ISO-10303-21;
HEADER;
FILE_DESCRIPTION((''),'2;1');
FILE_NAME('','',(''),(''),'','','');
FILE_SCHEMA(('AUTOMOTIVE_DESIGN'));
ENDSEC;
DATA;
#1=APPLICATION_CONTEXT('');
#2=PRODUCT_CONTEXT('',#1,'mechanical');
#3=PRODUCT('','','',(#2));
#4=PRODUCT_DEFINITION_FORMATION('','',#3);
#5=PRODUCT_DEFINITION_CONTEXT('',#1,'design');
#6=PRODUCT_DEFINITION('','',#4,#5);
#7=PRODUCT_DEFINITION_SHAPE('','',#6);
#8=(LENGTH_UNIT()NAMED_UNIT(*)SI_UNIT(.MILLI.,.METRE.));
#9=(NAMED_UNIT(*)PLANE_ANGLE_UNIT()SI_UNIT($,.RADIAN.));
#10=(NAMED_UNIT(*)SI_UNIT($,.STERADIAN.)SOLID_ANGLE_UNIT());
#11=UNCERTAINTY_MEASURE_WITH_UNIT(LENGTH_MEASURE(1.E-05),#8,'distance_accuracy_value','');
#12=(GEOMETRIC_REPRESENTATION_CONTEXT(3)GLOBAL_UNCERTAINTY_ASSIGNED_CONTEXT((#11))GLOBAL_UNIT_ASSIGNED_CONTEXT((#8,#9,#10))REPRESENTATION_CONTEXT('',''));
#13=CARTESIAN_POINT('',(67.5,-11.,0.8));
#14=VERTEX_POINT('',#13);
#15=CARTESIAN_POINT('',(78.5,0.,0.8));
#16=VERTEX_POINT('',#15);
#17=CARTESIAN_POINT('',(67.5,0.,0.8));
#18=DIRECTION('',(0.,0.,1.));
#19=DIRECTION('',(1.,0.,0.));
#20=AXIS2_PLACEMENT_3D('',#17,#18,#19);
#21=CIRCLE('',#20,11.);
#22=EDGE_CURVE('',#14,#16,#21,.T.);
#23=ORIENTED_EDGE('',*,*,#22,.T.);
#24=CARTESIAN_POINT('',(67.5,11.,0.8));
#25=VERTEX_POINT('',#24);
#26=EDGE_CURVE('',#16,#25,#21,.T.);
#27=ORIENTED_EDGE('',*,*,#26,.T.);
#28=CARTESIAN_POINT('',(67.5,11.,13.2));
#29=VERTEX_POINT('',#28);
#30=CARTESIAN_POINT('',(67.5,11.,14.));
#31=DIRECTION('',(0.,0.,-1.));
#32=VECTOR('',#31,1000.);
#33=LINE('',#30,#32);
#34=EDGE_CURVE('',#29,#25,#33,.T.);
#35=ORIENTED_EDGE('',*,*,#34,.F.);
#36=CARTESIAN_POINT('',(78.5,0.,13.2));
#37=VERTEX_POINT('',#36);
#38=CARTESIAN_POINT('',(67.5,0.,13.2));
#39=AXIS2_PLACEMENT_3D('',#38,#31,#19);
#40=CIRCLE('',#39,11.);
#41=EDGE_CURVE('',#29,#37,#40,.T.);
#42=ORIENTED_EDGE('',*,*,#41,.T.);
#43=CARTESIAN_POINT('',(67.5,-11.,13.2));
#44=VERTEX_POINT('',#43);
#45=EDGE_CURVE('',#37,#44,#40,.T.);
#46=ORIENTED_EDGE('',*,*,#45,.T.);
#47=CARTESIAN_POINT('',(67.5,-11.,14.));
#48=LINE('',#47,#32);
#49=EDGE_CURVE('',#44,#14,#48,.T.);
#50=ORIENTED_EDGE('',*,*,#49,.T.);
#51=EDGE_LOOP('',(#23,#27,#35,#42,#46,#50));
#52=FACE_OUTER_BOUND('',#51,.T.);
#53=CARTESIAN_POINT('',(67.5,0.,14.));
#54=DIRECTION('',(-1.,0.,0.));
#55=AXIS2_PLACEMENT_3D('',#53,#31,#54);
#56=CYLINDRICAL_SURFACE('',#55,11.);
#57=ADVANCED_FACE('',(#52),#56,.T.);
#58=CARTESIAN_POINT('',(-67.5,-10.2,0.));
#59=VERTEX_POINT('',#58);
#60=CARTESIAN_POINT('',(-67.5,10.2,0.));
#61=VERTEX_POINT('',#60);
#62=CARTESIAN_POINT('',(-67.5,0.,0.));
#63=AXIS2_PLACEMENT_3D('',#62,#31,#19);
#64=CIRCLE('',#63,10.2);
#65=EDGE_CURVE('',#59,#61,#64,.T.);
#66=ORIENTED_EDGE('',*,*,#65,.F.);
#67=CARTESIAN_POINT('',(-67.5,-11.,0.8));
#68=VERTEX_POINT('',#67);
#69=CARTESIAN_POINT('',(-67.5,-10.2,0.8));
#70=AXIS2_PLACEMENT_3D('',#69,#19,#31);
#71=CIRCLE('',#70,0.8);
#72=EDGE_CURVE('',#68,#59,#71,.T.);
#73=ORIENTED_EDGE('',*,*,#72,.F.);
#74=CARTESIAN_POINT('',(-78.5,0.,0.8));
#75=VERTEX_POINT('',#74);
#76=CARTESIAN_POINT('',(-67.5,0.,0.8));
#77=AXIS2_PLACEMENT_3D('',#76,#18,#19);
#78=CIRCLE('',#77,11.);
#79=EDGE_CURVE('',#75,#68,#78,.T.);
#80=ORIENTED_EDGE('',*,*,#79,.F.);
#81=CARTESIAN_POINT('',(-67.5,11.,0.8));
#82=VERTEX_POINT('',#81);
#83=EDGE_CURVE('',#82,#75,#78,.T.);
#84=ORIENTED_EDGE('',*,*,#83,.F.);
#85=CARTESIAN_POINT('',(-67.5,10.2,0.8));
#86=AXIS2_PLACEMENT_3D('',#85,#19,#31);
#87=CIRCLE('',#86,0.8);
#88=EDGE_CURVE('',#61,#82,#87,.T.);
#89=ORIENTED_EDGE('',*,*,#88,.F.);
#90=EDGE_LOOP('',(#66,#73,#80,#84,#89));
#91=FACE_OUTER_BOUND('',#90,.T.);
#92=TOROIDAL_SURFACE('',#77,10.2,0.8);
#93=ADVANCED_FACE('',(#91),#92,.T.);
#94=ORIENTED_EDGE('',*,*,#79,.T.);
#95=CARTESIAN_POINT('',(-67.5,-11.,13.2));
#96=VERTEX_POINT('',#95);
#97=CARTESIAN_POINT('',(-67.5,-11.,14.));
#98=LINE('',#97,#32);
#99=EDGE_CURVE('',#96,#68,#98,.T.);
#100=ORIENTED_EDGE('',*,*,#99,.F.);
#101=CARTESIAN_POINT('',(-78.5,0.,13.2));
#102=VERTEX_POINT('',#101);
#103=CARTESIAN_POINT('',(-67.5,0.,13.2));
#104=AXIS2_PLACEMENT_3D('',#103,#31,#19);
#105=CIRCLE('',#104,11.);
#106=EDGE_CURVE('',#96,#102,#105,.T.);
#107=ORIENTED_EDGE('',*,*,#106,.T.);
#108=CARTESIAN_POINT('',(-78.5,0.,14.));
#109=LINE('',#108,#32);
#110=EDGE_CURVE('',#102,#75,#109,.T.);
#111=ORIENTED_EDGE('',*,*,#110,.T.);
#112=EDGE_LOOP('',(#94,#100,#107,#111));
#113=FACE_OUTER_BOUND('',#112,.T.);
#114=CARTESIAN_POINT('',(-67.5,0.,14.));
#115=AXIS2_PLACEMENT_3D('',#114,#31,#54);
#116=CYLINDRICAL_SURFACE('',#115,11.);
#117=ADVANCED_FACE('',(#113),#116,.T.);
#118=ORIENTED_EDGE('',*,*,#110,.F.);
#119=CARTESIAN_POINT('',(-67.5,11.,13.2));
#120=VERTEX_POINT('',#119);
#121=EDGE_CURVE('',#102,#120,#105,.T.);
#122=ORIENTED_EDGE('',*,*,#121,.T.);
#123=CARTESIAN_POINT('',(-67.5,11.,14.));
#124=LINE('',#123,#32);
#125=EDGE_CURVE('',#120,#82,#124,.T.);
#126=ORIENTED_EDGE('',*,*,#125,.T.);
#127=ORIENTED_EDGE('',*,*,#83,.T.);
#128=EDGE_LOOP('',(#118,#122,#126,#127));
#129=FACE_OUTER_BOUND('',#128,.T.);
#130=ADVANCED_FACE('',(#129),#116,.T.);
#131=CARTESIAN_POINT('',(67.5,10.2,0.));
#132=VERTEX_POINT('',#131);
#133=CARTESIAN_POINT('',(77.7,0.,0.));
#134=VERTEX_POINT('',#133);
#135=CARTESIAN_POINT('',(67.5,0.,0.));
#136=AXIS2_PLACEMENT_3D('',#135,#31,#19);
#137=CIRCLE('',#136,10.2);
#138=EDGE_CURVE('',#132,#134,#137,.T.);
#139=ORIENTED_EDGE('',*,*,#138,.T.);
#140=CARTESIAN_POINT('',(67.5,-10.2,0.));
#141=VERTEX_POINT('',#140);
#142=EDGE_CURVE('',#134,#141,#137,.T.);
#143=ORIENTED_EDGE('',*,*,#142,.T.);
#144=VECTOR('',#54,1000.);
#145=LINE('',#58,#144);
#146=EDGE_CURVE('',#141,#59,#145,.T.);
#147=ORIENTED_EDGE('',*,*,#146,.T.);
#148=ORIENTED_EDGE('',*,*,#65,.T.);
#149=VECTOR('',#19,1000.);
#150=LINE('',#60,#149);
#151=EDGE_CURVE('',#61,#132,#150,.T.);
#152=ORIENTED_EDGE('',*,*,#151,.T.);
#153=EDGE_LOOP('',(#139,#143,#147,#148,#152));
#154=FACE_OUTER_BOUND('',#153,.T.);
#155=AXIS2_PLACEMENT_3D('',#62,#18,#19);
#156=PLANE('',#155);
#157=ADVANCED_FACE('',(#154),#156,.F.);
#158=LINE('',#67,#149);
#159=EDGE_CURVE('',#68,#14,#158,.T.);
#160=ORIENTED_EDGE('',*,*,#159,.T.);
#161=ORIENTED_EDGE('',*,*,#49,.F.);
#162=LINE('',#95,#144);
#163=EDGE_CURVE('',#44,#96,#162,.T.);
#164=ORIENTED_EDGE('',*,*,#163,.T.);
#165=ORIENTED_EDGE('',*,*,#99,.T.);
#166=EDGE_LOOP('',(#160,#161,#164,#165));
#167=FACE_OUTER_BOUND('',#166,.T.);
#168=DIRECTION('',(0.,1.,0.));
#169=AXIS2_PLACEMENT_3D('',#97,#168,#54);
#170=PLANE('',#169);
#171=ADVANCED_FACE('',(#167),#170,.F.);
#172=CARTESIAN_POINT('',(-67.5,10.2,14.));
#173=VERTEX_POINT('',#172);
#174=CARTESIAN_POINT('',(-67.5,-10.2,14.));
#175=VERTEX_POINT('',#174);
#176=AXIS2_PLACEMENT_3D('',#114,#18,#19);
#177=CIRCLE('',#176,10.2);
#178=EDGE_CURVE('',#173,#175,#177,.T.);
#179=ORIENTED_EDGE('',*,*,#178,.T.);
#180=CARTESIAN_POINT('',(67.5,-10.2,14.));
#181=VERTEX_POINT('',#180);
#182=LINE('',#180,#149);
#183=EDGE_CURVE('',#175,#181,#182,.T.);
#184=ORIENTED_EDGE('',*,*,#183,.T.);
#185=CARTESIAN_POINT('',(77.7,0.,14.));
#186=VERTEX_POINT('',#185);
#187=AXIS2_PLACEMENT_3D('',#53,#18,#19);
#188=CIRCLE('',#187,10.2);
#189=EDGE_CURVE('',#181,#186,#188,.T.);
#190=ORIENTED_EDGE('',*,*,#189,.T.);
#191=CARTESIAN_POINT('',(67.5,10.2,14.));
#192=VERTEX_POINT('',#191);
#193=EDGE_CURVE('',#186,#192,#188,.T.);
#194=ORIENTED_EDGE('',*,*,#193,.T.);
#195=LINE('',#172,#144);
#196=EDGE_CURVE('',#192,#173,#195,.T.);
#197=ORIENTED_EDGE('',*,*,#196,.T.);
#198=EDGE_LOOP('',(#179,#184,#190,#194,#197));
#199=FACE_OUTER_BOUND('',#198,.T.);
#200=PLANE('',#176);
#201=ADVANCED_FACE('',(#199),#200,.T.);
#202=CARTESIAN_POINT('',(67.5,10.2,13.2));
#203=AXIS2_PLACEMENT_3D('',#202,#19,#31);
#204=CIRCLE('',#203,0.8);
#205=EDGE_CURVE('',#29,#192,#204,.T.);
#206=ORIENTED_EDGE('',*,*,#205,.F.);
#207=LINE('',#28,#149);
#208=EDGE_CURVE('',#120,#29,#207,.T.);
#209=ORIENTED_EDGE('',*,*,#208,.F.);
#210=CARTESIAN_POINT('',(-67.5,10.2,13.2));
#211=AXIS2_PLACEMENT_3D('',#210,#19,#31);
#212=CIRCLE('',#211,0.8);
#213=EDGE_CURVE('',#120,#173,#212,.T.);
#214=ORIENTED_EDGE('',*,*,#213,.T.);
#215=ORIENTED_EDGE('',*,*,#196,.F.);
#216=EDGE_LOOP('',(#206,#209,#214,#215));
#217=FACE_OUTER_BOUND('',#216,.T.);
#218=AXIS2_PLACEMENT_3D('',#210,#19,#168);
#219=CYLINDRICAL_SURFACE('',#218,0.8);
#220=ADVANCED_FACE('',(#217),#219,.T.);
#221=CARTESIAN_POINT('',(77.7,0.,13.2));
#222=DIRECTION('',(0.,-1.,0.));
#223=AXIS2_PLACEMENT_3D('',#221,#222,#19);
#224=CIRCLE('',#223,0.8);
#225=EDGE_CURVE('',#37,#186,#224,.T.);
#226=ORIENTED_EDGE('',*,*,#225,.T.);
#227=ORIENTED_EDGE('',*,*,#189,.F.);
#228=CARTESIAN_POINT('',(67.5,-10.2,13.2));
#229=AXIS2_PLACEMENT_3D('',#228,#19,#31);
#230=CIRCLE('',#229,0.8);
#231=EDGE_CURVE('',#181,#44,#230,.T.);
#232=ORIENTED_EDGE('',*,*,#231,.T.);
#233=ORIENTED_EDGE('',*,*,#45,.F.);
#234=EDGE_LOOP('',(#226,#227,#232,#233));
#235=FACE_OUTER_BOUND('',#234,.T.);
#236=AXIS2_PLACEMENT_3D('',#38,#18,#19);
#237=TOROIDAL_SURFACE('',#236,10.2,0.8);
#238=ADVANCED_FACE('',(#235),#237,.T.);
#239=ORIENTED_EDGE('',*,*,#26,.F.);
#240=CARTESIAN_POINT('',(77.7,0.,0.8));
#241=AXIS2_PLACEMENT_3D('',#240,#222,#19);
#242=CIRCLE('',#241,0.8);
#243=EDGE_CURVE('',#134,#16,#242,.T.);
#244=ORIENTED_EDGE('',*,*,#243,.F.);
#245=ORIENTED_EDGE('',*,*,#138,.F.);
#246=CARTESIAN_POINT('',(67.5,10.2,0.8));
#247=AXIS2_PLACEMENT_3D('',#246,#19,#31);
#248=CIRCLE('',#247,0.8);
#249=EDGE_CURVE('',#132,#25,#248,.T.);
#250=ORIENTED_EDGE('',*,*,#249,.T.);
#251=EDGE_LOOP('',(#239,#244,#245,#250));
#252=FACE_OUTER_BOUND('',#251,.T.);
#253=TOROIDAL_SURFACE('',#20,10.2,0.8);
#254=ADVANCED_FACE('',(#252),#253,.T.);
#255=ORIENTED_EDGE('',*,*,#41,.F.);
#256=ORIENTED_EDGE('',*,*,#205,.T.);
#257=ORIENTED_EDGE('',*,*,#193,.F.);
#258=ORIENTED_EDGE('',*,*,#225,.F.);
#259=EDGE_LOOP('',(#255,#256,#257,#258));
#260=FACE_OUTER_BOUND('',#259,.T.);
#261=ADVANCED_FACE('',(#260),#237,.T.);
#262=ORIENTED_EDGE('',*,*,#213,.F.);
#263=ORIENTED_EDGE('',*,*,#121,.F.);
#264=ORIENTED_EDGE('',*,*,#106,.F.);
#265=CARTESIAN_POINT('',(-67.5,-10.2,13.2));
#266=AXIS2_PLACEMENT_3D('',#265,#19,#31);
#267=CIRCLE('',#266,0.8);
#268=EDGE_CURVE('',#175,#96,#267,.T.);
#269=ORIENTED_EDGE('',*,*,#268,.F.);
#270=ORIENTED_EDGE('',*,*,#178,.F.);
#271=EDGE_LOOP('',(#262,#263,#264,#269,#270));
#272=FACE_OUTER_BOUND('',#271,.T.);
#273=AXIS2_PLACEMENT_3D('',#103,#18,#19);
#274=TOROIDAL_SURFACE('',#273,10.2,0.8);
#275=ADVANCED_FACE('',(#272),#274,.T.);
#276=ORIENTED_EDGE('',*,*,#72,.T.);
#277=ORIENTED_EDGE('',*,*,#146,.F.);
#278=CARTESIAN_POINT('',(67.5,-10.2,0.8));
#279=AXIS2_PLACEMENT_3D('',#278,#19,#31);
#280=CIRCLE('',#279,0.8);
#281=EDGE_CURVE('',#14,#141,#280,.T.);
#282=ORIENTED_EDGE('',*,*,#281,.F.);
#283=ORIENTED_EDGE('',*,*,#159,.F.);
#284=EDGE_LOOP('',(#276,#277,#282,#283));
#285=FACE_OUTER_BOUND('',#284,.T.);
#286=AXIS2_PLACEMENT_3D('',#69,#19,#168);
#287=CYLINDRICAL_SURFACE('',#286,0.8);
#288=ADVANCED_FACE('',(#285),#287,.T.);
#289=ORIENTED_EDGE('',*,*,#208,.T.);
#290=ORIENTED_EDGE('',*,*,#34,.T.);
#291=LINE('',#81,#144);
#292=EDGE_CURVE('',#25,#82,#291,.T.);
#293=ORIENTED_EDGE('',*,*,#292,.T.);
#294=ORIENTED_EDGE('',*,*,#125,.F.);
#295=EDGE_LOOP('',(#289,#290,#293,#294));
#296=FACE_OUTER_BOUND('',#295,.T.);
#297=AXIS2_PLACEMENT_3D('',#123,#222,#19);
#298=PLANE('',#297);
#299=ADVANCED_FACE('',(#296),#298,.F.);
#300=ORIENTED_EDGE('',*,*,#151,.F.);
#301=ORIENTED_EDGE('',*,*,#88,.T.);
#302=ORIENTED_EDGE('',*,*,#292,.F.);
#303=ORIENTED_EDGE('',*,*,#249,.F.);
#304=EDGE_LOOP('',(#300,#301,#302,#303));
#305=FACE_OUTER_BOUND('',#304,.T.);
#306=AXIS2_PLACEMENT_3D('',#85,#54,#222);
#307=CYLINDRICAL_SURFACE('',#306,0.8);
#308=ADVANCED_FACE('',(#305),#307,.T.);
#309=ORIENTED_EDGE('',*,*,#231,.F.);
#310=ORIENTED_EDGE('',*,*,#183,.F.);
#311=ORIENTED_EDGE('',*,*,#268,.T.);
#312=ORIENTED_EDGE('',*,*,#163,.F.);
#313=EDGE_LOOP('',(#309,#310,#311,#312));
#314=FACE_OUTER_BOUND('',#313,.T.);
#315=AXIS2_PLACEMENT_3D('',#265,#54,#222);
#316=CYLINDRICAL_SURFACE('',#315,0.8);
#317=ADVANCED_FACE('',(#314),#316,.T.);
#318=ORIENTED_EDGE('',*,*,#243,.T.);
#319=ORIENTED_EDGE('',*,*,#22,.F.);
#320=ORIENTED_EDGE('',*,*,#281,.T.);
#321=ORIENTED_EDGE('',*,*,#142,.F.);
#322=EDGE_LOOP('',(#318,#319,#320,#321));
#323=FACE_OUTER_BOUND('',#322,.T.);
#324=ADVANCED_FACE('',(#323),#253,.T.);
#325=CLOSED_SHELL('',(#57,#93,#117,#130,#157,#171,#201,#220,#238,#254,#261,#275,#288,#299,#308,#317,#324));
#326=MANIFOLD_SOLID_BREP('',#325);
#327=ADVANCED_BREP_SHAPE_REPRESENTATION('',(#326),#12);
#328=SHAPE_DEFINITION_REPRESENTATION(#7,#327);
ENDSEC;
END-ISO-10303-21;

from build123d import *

# Parameters (mm, degrees)
BOSS_EXTRUDE1_DEPTH = 14
FILLET1_R           = 0.8


with BuildPart() as part:
    # Sketch1 → Boss-Extrude1 (new body)
    with BuildSketch(Plane.XY):
        with BuildLine():
            Line((-67.5, 11), (67.5, 11))
            ThreePointArc((67.5, 11), (78.5, 0), (67.5, -11))
            Line((67.5, -11), (-67.5, -11))
            ThreePointArc((-67.5, -11), (-78.5, 0), (-67.5, 11))
        make_face()
    extrude(amount=BOSS_EXTRUDE1_DEPTH)

    # Fillet1
    fillet1_edges = [part.edges().sort_by_distance(p)[0] for p in [
        (78.5, 0, 14),
        (0, 11, 14),
        (-78.5, 0, 14),
        (0, 11, 0),
        (78.5, 0, 0),
        (0, -11, 0),
        (-78.5, 0, 0),
        (0, -11, 14),
    ]]
    fillet(fillet1_edges, radius=FILLET1_R)


solid = part.part
